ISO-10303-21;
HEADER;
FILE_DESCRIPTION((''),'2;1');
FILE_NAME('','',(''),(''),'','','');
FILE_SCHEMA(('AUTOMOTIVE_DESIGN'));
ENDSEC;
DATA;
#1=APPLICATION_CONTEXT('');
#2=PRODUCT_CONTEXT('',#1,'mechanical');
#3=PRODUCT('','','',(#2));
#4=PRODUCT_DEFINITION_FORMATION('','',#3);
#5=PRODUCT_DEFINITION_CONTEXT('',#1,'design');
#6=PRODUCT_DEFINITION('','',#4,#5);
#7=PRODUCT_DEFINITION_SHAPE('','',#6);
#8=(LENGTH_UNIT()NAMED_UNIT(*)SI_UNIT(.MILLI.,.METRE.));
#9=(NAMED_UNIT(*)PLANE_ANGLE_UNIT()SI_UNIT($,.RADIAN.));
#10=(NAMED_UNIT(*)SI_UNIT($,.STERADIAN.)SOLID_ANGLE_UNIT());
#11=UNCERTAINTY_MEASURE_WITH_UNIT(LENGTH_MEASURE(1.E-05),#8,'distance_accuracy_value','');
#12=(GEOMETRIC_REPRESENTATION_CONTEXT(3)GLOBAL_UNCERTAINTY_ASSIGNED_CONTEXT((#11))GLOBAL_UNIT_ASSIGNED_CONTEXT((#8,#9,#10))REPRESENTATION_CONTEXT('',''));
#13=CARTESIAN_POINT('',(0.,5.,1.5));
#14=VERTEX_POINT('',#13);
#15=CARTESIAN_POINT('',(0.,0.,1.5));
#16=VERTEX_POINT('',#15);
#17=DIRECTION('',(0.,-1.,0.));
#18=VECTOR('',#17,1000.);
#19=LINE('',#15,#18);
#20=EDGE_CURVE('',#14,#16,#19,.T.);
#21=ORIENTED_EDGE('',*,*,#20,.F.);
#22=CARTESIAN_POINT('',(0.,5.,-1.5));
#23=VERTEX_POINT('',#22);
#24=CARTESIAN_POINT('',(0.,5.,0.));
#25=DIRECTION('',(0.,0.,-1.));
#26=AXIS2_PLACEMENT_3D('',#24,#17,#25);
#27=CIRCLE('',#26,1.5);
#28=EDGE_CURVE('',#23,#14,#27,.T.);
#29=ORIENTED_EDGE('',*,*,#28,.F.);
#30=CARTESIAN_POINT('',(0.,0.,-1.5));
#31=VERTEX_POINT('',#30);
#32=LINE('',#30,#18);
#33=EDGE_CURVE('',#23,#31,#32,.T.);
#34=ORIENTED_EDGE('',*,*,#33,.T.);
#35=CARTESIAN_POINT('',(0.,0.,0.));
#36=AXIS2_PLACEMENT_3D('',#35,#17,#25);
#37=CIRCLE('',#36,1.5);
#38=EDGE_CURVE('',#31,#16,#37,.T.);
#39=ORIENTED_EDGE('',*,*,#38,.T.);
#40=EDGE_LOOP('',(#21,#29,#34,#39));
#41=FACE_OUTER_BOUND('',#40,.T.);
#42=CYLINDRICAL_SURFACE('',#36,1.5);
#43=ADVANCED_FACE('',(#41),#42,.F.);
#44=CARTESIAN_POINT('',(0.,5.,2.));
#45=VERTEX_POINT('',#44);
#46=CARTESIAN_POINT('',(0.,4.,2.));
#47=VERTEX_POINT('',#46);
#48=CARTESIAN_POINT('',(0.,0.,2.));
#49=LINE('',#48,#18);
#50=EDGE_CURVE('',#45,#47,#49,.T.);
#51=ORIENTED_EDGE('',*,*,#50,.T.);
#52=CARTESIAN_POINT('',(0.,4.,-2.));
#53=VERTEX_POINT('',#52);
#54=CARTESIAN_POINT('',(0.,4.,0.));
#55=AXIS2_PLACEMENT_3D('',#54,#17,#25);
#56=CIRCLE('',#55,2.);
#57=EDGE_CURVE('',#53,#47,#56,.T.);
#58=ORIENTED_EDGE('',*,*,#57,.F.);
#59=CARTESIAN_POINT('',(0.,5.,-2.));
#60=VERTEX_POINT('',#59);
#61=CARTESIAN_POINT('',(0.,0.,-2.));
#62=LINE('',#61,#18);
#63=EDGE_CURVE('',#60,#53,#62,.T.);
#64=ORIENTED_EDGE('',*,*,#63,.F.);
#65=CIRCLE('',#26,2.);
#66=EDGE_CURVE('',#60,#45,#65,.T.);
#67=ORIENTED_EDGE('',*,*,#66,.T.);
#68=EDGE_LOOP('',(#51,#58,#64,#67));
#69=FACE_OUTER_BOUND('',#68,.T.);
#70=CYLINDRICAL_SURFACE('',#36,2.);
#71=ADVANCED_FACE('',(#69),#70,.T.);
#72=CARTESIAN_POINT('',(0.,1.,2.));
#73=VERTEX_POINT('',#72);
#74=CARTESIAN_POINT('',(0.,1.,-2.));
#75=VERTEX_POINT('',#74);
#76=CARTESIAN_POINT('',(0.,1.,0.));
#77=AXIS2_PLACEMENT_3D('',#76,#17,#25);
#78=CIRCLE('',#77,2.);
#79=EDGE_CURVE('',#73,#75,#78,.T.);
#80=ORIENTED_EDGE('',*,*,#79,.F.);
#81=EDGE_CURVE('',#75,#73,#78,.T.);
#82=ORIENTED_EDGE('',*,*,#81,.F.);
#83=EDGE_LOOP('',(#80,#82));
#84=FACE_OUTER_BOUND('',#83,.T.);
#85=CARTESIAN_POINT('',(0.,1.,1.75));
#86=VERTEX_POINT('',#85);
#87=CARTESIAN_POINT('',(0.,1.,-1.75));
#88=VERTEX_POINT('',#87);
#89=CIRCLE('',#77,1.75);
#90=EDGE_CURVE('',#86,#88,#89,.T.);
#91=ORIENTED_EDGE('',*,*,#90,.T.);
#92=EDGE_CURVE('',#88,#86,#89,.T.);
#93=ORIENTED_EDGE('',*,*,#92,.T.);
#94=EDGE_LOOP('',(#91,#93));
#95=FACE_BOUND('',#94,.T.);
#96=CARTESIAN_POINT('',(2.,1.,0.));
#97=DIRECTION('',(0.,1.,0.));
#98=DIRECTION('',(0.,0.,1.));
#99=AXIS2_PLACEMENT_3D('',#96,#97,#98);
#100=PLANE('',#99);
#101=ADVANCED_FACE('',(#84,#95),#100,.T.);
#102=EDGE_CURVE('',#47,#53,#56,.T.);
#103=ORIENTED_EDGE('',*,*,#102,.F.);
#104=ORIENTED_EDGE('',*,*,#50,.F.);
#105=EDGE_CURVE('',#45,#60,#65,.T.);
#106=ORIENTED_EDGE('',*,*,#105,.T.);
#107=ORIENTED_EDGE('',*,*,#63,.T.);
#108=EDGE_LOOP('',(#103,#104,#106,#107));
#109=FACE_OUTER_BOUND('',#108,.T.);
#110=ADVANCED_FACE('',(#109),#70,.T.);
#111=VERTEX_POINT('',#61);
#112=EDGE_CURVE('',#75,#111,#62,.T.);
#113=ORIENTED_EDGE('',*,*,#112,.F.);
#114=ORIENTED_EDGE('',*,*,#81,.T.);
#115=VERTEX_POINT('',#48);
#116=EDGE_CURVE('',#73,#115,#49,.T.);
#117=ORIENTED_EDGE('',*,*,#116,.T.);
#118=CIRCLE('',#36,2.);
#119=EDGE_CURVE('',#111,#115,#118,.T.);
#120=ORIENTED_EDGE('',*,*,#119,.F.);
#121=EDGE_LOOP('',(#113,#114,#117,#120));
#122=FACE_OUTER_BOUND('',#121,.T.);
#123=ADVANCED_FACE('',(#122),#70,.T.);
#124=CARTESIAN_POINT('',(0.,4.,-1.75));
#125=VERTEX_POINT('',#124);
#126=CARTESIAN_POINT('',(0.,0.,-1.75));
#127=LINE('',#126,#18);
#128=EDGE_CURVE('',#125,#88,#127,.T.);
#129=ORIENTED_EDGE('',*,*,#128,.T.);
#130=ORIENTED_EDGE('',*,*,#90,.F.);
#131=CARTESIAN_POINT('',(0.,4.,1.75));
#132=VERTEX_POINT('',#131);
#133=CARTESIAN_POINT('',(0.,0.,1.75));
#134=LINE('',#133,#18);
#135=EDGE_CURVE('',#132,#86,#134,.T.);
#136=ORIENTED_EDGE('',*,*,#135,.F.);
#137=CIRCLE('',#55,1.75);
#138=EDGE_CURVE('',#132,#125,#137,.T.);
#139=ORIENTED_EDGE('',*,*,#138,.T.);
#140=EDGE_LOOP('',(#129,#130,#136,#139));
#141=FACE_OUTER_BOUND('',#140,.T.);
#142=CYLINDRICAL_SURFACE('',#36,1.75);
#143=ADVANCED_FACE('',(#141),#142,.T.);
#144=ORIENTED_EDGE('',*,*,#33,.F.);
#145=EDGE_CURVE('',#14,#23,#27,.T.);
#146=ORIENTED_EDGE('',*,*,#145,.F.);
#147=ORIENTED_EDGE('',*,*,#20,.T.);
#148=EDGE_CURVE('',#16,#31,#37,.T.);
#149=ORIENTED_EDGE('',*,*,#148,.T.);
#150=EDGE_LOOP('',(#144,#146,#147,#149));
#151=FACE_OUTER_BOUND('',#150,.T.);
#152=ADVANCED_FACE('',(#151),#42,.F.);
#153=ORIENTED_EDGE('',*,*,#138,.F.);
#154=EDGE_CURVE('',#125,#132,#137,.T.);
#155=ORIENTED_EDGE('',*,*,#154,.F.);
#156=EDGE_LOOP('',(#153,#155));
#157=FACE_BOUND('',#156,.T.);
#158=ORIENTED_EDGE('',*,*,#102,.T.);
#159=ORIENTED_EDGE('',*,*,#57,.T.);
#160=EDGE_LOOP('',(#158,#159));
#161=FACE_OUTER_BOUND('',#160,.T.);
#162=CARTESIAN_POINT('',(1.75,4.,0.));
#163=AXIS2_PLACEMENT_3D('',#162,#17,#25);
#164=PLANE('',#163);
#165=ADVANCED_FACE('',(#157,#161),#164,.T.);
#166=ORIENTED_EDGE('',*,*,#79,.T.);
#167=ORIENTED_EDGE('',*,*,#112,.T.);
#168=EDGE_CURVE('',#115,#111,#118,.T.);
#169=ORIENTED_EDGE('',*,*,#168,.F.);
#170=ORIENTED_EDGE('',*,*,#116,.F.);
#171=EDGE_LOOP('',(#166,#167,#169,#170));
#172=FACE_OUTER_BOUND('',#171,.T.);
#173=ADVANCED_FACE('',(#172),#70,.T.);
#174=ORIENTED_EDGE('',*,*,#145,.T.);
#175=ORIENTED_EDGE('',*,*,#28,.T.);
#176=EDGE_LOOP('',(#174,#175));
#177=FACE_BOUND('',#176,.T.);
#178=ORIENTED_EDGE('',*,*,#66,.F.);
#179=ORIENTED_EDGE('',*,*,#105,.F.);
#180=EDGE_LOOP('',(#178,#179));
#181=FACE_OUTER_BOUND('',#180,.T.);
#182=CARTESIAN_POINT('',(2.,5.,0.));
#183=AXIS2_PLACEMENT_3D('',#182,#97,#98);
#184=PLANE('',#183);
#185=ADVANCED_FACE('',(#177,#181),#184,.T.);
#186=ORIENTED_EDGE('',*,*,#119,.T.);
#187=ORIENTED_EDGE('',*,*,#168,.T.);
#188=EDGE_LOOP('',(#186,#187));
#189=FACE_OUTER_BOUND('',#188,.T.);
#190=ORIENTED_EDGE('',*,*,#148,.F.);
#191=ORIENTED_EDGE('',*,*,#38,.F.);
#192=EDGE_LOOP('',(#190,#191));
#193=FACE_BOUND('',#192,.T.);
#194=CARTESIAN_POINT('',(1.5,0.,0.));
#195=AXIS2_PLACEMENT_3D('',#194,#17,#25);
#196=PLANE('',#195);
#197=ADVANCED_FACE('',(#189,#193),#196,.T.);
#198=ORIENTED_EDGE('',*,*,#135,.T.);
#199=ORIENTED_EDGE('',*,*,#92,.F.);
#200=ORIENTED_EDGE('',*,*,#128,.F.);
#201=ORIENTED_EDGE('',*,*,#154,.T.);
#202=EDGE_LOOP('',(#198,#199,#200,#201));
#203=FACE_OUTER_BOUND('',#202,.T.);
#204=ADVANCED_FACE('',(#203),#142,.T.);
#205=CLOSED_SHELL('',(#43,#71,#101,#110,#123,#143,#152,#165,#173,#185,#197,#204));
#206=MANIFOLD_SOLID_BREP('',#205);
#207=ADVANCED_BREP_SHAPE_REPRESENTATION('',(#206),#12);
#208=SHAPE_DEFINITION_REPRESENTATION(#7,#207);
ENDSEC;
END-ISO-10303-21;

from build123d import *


with BuildPart() as part:
    # Sketch1 → Revolve1 (revolve)
    with BuildSketch(Plane.XY, mode=Mode.PRIVATE) as revolve1_sk:
        Polygon((1.5, 0), (2, 0), (2, 1), (1.75, 1), (1.75, 4), (2, 4), (2, 5), (1.5, 5), align=None)
    revolve(revolve1_sk.sketch.rotate(Axis((0, 0, 0), (0, 1, 0)), 90), axis=Axis((0, 0, 0), (0, 1, 0)))


solid = part.part
